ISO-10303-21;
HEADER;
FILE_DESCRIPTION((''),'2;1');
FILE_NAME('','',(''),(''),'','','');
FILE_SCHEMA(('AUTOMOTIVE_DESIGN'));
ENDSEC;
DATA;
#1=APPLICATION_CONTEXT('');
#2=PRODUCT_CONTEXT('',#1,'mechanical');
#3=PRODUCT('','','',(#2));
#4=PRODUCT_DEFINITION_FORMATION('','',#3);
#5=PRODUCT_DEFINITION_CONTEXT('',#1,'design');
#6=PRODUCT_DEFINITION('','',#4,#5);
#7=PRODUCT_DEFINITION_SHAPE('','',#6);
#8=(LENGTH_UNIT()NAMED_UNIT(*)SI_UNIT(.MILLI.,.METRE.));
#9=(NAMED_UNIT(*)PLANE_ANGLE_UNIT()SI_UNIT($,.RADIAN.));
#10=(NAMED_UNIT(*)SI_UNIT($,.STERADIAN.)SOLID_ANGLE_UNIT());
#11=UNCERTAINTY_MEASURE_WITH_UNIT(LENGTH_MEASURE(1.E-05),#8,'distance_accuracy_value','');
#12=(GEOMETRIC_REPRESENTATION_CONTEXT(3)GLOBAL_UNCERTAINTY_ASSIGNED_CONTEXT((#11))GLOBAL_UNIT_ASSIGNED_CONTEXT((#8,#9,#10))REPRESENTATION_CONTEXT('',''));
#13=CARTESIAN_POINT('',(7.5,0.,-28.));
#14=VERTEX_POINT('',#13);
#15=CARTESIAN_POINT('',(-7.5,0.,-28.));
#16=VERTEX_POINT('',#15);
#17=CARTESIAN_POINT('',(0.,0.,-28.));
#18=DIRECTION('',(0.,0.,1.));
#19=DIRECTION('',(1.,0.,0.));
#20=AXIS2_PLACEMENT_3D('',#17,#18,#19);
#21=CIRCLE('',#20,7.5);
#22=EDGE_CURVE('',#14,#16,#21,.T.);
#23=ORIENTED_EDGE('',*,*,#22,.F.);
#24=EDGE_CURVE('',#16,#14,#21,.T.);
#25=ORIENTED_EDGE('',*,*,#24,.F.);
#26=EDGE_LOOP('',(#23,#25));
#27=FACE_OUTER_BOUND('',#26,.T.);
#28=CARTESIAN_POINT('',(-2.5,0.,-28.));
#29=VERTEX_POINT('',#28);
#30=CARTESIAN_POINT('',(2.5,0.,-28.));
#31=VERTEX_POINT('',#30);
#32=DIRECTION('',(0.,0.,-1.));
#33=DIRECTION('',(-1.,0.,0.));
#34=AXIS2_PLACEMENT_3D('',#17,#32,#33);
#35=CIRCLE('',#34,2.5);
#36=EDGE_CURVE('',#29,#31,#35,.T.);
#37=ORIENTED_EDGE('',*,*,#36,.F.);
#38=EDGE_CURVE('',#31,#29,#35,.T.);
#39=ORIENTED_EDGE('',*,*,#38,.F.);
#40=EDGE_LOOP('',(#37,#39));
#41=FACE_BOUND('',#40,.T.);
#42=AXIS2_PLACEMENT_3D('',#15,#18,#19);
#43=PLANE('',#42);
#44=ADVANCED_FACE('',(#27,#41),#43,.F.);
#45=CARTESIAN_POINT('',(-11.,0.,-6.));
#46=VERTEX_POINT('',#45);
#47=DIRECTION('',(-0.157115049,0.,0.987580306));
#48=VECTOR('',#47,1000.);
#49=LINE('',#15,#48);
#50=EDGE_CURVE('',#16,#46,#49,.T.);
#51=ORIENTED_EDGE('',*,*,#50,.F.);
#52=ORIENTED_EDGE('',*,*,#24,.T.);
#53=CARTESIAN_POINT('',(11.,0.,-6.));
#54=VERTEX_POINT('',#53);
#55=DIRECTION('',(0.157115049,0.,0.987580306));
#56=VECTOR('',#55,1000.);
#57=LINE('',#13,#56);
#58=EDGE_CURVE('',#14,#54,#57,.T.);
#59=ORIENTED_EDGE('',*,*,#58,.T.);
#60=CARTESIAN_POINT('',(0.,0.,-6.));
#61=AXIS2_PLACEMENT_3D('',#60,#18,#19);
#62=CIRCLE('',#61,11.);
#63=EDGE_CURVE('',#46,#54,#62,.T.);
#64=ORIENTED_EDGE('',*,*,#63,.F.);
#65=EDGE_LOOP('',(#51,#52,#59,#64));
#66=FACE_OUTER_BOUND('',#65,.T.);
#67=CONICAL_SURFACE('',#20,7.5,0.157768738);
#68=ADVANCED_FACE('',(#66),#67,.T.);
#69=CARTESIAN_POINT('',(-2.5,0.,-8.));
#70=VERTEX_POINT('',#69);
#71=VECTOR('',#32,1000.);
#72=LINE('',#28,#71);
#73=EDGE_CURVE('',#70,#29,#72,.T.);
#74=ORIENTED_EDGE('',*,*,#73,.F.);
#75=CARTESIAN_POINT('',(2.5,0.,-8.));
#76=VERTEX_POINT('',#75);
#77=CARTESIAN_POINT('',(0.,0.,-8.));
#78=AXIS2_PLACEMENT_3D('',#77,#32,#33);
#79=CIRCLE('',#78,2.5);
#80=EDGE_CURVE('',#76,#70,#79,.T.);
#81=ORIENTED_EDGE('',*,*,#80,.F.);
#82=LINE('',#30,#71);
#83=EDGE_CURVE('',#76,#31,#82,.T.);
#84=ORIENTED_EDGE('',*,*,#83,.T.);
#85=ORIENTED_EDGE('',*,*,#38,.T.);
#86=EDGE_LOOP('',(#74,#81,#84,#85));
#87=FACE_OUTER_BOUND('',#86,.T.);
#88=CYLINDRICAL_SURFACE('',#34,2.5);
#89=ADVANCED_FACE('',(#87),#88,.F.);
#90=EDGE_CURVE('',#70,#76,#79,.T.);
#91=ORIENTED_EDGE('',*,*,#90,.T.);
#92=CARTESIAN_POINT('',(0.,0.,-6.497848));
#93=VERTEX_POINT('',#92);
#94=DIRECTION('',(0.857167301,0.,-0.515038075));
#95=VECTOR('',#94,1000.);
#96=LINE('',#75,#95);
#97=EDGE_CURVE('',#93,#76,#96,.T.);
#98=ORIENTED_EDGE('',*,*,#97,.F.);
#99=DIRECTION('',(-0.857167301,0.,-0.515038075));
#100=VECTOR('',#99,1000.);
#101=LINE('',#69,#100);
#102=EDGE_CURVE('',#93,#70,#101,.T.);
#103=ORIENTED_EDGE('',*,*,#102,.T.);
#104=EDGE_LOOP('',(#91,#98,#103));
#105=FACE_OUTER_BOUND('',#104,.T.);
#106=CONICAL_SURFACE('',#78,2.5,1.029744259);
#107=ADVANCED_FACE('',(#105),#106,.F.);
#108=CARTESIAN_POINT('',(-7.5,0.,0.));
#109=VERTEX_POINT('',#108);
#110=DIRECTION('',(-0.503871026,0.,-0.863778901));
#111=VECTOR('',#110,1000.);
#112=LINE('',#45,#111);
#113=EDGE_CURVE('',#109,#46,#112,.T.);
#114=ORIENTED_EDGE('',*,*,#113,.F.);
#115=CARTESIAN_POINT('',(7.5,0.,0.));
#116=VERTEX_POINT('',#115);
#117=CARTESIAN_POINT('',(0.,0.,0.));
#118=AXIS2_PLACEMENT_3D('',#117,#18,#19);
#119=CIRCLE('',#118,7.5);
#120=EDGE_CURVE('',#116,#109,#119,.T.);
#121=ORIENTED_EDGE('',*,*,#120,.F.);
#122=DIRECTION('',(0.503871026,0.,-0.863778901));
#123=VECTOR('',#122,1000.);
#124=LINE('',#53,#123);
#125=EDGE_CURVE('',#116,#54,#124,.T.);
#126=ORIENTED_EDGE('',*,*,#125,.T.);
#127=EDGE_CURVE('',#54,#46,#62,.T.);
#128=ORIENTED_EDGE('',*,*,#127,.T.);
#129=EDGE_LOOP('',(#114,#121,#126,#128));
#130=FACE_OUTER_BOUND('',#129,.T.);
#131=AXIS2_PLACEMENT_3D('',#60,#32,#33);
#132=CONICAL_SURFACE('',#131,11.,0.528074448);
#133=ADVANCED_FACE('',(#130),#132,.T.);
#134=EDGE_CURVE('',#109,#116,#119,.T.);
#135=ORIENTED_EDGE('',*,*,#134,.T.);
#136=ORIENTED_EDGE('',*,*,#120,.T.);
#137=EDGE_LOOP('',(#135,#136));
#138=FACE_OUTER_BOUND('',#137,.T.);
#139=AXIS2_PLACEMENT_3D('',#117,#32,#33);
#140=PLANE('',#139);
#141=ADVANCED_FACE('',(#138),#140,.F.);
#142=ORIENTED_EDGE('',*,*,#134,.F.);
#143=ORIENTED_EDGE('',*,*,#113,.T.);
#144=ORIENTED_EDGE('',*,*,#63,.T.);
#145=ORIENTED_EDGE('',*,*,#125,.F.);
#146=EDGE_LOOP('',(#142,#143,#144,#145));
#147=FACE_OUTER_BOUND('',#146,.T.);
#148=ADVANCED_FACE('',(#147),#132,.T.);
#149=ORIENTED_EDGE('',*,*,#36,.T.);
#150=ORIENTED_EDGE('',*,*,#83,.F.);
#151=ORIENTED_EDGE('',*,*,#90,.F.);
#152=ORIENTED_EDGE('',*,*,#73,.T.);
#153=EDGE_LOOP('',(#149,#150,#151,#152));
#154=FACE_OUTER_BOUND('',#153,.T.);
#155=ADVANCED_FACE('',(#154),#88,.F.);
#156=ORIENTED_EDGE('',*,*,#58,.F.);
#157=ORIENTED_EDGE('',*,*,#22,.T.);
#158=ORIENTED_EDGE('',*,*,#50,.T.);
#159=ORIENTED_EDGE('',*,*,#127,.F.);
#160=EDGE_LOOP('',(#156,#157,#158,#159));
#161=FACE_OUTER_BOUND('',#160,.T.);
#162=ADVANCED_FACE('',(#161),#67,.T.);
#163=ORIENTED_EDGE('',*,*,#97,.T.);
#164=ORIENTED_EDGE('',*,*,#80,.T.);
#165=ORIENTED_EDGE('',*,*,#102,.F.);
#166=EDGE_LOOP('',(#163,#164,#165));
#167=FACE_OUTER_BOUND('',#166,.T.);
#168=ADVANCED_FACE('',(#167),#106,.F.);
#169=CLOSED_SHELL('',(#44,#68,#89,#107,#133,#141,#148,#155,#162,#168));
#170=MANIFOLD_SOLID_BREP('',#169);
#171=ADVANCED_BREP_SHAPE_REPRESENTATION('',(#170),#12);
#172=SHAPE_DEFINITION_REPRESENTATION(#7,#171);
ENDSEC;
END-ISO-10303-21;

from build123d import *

# Parameters (mm, degrees)
M6_TAPPED_HOLE1_D     = 5
M6_TAPPED_HOLE1_DEPTH = 20
M6_TAPPED_HOLE1_TIP   = 1.502151548


with BuildPart() as part:
    # Sketch1 → Revolve1 (revolve)
    with BuildSketch(Plane(origin=(0, 0, 0), x_dir=(1, 0, 0), z_dir=(0, 1, 0)), mode=Mode.PRIVATE) as revolve1_sk:
        Polygon((0, 0), (-7.5, 0), (-11, 6), (-7.5, 28), (0, 28), align=None)
    revolve(revolve1_sk.sketch.rotate(Axis((0, 0, 0), (0, 0, -1)), 180), axis=Axis((0, 0, 0), (0, 0, -1)))

    # M6 Tapped Hole1
    with Locations(Plane(origin=(0, 0, -28), x_dir=(-1, 0, 0), z_dir=(0, 0, -1))):
        with Locations((0, 0)):
            Hole(M6_TAPPED_HOLE1_D / 2, depth=M6_TAPPED_HOLE1_DEPTH)
            with Locations((0, 0, -(M6_TAPPED_HOLE1_DEPTH + M6_TAPPED_HOLE1_TIP / 2))):  # 118° drill point
                Cone(0, M6_TAPPED_HOLE1_D / 2, M6_TAPPED_HOLE1_TIP, mode=Mode.SUBTRACT)


solid = part.part
